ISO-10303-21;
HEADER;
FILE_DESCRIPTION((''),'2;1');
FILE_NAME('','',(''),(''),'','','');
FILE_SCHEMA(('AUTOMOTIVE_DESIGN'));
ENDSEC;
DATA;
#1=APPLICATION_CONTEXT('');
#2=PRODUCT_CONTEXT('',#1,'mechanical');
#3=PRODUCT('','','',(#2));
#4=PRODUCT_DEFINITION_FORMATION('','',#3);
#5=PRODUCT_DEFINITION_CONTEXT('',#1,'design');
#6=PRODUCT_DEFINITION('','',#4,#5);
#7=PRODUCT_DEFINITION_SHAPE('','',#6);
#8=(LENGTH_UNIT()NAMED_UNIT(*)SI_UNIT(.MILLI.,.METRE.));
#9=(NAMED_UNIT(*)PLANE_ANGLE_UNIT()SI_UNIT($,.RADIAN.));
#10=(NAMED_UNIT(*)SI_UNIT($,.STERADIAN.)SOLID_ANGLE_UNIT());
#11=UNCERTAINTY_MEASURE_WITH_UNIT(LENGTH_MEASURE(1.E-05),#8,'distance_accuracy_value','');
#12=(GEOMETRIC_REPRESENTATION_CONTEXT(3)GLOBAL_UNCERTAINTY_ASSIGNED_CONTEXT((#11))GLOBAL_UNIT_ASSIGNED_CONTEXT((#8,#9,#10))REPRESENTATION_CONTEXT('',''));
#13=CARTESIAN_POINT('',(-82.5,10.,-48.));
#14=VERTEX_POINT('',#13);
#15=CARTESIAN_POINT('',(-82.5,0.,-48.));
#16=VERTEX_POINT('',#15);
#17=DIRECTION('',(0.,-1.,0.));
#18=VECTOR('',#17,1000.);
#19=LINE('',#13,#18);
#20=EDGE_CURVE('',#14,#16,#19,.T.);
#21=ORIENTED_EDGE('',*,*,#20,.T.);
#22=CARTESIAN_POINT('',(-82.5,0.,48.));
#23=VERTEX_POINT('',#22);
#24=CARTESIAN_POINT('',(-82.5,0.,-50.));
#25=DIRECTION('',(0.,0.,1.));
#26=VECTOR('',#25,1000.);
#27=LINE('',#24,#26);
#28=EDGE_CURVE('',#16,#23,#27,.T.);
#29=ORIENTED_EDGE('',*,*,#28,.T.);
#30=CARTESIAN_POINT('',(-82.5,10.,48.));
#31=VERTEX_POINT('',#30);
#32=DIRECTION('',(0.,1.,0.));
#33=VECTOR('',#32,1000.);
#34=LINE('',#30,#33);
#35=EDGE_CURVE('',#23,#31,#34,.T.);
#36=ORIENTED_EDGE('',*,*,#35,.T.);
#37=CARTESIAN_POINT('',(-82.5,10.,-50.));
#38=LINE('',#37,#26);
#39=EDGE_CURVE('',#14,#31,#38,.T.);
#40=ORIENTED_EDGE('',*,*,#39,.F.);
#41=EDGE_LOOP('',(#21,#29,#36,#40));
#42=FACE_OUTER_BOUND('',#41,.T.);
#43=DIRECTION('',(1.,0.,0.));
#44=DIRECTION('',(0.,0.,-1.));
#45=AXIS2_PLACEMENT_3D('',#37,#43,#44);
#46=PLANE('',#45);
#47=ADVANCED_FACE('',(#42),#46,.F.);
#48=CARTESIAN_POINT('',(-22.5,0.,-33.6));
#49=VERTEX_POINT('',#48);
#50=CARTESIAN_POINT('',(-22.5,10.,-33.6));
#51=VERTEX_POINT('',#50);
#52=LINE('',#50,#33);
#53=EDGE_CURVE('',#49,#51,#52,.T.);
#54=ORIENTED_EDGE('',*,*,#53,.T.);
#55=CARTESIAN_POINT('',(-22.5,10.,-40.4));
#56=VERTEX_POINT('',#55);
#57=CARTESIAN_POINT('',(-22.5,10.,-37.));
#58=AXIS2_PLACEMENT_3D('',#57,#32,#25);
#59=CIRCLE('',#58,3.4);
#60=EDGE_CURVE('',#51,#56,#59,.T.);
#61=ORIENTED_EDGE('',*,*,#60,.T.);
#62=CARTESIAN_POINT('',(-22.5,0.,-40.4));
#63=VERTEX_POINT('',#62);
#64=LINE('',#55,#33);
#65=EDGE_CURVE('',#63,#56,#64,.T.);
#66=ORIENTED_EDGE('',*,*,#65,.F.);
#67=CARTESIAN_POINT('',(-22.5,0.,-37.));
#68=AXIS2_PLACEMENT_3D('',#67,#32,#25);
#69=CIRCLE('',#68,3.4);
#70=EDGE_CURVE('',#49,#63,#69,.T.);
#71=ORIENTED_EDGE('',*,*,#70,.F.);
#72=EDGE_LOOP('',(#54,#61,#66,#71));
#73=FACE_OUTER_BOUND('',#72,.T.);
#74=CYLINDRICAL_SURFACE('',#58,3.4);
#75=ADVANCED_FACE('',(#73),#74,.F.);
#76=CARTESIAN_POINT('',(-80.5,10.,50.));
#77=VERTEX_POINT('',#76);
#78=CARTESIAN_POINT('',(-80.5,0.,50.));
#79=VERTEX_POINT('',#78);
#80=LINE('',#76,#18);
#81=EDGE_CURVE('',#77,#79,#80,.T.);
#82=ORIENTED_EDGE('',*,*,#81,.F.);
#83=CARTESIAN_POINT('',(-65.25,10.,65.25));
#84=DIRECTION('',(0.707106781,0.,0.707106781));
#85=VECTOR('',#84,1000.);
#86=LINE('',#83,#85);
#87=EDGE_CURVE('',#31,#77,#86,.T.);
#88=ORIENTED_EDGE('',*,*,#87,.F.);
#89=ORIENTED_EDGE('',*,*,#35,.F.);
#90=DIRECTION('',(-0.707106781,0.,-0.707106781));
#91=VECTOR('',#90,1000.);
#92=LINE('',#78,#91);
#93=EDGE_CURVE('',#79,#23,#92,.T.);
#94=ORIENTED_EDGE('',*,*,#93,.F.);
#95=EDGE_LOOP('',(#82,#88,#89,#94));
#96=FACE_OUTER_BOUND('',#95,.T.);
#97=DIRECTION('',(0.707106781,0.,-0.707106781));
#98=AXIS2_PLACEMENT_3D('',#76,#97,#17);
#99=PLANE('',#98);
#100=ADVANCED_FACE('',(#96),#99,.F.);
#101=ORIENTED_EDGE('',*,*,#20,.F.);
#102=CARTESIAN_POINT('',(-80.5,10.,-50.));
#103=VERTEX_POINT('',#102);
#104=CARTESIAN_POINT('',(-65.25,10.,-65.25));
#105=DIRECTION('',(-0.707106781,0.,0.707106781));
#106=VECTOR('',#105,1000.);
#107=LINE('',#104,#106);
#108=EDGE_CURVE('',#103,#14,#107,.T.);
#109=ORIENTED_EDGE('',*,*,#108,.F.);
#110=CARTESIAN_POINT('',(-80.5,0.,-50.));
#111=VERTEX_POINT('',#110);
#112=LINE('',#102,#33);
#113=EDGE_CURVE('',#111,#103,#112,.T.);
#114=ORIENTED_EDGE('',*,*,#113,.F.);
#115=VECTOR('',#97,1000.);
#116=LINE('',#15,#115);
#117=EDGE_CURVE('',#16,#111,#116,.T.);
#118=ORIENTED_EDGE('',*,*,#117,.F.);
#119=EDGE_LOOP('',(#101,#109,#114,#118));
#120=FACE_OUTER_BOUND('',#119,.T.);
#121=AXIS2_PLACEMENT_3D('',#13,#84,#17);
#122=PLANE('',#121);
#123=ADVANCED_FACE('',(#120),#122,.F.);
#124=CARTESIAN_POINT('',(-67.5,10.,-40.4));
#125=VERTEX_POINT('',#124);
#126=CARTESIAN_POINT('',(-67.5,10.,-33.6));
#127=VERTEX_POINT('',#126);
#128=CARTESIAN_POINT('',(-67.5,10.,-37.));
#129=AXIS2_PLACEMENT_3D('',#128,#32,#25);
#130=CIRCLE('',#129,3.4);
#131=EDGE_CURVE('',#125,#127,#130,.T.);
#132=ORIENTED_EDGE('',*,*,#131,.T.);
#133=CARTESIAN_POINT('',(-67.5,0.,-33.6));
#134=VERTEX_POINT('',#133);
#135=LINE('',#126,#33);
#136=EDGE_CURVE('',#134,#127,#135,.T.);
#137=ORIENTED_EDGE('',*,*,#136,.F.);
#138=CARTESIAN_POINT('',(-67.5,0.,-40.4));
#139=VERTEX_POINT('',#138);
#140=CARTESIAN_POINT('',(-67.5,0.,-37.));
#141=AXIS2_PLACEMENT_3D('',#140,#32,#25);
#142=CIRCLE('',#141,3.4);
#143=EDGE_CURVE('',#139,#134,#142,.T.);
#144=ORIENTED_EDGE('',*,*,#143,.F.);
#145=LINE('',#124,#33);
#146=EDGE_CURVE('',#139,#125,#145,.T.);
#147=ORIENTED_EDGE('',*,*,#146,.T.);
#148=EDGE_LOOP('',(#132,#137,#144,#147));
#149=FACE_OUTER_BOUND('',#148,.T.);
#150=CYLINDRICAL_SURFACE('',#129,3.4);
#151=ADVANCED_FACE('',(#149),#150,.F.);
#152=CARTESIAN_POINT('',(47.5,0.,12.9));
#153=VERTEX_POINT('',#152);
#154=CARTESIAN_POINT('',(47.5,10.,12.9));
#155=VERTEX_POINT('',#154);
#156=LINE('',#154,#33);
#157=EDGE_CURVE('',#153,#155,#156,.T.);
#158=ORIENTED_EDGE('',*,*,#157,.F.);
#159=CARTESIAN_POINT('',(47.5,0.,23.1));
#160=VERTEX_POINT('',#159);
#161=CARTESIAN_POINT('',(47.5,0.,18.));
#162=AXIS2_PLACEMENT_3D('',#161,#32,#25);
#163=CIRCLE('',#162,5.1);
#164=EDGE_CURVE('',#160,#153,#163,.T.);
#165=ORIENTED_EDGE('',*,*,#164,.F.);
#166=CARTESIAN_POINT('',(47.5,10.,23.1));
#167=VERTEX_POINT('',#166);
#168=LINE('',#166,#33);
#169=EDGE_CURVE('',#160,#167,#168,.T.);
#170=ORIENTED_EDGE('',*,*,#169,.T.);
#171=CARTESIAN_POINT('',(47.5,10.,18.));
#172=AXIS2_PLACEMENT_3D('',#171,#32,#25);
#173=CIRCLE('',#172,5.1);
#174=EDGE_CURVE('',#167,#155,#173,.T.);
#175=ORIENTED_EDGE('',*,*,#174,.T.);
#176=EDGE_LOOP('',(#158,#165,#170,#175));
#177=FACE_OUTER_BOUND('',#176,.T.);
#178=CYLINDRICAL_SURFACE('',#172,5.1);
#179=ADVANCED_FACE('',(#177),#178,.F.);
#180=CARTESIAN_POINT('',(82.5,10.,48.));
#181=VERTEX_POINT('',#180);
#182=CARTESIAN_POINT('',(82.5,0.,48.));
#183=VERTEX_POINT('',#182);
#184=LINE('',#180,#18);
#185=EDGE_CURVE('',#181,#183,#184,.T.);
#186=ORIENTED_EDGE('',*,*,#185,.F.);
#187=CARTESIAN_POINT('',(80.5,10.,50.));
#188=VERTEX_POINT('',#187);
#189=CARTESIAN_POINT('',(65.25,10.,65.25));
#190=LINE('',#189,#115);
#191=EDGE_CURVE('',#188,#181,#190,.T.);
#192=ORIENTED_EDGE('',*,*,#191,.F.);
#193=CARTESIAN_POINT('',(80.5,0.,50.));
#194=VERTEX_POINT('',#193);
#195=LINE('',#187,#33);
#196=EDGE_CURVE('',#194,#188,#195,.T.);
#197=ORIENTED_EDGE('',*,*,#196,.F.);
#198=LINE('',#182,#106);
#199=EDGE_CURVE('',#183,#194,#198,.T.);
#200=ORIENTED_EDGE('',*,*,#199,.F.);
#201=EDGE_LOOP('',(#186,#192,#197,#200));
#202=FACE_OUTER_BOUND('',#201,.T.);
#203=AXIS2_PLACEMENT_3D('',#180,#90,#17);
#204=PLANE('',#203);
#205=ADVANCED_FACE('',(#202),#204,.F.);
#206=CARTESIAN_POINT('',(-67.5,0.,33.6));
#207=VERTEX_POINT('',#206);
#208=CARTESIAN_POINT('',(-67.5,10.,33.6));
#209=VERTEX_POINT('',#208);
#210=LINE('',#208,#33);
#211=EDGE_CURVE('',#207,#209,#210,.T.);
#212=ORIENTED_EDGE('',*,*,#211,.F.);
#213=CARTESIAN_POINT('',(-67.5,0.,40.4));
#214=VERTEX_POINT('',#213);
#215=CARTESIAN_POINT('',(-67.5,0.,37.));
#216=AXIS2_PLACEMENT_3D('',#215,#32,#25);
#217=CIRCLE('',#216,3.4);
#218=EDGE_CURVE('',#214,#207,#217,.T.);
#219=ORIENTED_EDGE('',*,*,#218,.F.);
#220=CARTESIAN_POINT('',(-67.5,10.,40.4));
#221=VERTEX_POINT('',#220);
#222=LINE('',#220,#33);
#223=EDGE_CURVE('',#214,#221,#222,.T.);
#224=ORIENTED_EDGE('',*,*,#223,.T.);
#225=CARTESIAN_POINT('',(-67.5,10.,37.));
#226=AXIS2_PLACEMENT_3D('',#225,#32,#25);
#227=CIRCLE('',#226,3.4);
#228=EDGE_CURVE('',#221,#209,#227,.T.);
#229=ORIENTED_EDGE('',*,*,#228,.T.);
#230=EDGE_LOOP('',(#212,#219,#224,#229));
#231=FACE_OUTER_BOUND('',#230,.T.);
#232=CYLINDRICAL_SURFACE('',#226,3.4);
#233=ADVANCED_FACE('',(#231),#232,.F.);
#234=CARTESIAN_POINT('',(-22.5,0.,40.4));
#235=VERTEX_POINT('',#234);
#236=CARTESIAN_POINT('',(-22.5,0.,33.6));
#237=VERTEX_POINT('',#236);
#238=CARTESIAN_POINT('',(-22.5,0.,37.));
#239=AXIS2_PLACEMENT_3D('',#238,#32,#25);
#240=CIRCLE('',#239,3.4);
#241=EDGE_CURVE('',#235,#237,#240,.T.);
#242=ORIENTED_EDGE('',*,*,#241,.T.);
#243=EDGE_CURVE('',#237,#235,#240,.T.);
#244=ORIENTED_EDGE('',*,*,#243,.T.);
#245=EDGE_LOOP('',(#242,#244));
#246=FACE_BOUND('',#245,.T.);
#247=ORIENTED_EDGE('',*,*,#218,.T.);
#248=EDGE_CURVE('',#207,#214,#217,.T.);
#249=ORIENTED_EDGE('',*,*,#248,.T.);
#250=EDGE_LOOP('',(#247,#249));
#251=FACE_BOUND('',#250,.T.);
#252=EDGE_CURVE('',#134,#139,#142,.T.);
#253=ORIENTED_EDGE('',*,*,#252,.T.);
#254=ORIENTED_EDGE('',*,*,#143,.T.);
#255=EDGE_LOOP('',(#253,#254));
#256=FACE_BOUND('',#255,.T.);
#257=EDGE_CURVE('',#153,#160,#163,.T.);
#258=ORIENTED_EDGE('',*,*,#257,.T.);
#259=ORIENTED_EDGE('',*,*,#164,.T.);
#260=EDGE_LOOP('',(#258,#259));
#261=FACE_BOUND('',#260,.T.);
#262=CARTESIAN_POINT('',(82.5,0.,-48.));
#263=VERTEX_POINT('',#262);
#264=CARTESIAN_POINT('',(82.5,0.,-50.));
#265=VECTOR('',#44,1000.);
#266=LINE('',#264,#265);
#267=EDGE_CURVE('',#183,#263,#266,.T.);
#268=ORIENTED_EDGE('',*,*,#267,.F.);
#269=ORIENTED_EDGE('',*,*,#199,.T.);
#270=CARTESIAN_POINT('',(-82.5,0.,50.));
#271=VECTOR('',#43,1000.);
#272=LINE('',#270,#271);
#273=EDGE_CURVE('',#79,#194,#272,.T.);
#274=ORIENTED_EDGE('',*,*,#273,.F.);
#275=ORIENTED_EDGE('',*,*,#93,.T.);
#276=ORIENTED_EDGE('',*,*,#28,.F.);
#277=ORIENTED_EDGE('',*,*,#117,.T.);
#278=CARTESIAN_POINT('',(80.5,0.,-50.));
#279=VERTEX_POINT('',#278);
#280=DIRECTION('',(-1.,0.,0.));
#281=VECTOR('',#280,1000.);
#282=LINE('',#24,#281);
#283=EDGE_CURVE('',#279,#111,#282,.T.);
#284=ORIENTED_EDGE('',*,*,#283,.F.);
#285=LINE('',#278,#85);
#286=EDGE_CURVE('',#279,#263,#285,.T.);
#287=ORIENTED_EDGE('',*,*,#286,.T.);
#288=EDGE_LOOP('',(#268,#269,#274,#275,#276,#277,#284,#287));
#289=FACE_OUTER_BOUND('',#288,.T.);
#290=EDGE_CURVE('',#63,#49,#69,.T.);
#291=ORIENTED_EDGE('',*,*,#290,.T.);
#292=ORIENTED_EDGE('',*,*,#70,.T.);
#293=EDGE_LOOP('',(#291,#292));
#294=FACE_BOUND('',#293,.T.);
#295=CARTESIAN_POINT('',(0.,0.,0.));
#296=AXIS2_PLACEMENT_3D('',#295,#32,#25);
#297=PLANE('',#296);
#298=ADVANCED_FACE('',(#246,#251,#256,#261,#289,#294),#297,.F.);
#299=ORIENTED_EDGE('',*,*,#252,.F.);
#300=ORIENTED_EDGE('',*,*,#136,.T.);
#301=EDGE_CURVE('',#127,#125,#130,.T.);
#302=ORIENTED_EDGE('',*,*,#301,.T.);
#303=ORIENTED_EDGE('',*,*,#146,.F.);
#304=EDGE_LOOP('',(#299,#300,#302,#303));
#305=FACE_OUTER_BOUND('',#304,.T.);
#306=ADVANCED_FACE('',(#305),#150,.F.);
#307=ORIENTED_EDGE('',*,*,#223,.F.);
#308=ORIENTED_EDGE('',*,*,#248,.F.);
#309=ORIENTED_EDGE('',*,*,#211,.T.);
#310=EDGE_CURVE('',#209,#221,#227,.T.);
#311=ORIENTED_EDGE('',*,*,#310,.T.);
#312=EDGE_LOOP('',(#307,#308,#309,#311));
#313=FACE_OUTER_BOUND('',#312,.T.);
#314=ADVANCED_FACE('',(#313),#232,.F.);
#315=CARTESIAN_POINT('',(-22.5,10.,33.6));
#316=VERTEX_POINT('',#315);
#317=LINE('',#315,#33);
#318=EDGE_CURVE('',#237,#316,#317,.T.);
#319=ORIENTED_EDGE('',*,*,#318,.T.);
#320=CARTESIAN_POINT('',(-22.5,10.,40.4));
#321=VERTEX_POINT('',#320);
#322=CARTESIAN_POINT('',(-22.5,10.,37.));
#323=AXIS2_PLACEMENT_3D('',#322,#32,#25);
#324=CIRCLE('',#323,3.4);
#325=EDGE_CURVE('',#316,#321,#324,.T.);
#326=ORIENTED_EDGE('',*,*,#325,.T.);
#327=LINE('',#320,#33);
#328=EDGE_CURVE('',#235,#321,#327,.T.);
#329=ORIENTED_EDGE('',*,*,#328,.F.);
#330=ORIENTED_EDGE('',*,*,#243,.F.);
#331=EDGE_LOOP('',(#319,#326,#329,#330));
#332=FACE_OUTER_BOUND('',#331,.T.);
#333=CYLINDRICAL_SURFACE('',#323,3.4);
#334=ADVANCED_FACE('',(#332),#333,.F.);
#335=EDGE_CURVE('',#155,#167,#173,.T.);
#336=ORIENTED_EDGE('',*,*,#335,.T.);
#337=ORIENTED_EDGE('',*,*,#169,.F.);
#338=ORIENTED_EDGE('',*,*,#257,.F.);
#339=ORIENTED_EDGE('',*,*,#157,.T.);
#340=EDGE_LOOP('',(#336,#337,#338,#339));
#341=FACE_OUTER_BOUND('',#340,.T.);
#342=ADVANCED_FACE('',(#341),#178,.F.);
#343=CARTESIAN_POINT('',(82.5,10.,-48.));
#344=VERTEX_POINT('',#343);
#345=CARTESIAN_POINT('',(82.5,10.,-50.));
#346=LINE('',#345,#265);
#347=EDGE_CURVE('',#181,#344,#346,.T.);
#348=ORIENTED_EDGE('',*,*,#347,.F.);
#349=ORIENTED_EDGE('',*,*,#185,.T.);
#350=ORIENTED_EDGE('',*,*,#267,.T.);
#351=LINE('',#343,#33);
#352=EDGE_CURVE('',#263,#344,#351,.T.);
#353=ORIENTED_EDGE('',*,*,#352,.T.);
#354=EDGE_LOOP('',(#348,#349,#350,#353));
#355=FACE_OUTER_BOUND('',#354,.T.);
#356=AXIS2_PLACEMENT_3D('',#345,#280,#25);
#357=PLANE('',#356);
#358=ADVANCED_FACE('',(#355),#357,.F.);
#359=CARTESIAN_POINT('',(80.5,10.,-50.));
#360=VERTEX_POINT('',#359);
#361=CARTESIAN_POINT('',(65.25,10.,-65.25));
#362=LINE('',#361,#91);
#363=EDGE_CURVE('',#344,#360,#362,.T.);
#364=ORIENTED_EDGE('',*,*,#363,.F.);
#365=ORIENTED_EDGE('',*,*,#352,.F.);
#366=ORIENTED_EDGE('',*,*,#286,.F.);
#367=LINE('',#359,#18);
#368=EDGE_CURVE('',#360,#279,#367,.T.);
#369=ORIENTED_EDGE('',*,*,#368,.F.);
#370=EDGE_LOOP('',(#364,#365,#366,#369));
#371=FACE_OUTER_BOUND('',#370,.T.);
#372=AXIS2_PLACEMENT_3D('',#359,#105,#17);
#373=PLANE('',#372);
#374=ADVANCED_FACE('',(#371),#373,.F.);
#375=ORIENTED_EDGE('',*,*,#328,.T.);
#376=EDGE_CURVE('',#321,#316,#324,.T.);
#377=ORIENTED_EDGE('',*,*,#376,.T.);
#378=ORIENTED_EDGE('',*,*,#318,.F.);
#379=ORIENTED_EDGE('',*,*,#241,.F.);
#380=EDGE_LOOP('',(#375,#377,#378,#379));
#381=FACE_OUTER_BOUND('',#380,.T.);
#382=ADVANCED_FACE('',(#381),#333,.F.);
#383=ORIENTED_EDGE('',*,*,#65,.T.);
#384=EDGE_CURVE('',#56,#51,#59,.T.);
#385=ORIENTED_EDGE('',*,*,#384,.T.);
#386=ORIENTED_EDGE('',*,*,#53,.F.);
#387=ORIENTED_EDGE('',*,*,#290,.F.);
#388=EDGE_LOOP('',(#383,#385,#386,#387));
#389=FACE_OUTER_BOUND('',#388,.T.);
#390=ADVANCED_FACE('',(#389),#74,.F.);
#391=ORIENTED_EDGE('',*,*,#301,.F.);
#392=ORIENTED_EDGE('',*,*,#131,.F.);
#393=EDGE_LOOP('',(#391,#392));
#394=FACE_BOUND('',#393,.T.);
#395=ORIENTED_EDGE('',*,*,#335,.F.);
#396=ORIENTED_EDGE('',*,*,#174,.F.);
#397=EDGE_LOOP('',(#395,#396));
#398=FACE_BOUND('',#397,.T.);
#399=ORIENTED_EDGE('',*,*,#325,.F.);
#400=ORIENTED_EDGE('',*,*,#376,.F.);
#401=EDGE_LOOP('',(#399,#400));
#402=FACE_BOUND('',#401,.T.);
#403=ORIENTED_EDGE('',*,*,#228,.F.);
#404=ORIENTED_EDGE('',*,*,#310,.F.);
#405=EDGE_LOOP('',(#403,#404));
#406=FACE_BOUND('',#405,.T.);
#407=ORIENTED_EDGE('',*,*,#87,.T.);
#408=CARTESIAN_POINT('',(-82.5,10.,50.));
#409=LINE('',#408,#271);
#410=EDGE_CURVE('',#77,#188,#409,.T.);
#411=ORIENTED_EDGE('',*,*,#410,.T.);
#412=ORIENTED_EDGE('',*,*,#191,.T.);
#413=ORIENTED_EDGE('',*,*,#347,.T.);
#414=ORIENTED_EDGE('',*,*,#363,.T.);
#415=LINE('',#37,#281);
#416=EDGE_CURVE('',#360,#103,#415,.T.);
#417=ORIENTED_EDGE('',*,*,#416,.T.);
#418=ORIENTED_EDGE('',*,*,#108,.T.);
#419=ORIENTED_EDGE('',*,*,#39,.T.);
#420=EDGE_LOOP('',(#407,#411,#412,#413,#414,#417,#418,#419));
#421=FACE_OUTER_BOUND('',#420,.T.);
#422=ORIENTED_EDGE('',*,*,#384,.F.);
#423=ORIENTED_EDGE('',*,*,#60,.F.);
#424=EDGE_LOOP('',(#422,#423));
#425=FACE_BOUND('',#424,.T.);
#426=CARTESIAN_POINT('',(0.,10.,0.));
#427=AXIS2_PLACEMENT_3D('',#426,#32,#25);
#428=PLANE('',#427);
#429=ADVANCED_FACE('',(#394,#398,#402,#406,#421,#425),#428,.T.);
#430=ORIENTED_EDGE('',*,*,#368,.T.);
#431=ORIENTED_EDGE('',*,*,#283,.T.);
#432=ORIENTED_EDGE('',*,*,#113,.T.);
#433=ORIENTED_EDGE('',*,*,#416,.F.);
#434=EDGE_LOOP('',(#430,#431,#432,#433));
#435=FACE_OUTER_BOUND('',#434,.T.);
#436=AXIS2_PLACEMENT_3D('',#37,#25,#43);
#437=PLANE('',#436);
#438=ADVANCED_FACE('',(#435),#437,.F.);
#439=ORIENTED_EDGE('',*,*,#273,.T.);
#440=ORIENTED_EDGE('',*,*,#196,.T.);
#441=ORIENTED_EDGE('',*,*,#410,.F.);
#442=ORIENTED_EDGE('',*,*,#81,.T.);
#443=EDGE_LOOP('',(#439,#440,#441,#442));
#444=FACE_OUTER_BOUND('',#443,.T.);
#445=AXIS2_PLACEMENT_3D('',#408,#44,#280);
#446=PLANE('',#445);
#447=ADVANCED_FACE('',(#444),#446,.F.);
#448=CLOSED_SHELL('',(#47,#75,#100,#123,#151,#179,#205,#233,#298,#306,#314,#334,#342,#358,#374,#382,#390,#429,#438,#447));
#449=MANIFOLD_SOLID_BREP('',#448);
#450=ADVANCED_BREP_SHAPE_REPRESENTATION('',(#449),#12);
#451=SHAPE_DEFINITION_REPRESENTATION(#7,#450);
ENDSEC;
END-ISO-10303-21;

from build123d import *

# Parameters (mm, degrees)
SKETCH_1_W              = 165
SKETCH_1_H              = 100
EXTRUDE_1_DEPTH         = 10
HOLE_WIZARD_M8_1_D      = 6.8
HOLE_WIZARD_M8_1_DEPTH  = 16.25
HOLE_WIZARD_M8_1_TIP    = 2.042926105
HOLE_WIZARD_M12_1_D     = 10.2
HOLE_WIZARD_M12_1_DEPTH = 32.75
HOLE_WIZARD_M12_1_TIP   = 3.064389157
CHAMFER_1_SIZE          = 2


with BuildPart() as part:
    # 草图1 → 凸台-拉伸1 (new body)
    with BuildSketch(Plane(origin=(0, 0, 0), x_dir=(1, 0, 0), z_dir=(0, 1, 0))):
        Rectangle(SKETCH_1_W, SKETCH_1_H)
    extrude(amount=EXTRUDE_1_DEPTH)

    # M8 螺纹孔1
    with Locations(Plane(origin=(0, 10, 0), x_dir=(1, 0, 0), z_dir=(0, 1, 0))):
        with Locations((-67.5, 37), (-22.5, 37), (-22.5, -37), (-67.5, -37)):
            Hole(HOLE_WIZARD_M8_1_D / 2, depth=HOLE_WIZARD_M8_1_DEPTH)
            with Locations((0, 0, -(HOLE_WIZARD_M8_1_DEPTH + HOLE_WIZARD_M8_1_TIP / 2))):  # 118° drill point
                Cone(0, HOLE_WIZARD_M8_1_D / 2, HOLE_WIZARD_M8_1_TIP, mode=Mode.SUBTRACT)

    # M12 螺纹孔1
    with Locations(Plane(origin=(0, 10, 0), x_dir=(1, 0, 0), z_dir=(0, 1, 0))):
        with Locations((47.5, -18)):
            Hole(HOLE_WIZARD_M12_1_D / 2, depth=HOLE_WIZARD_M12_1_DEPTH)
            with Locations((0, 0, -(HOLE_WIZARD_M12_1_DEPTH + HOLE_WIZARD_M12_1_TIP / 2))):  # 118° drill point
                Cone(0, HOLE_WIZARD_M12_1_D / 2, HOLE_WIZARD_M12_1_TIP, mode=Mode.SUBTRACT)

    # 倒角1
    chamfer_1_edges = [part.edges().sort_by_distance(p)[0] for p in [
        (82.5, 5, 50),
        (-82.5, 5, 50),
        (-82.5, 5, -50),
        (82.5, 5, -50),
    ]]
    chamfer(chamfer_1_edges, length=CHAMFER_1_SIZE)


solid = part.part
